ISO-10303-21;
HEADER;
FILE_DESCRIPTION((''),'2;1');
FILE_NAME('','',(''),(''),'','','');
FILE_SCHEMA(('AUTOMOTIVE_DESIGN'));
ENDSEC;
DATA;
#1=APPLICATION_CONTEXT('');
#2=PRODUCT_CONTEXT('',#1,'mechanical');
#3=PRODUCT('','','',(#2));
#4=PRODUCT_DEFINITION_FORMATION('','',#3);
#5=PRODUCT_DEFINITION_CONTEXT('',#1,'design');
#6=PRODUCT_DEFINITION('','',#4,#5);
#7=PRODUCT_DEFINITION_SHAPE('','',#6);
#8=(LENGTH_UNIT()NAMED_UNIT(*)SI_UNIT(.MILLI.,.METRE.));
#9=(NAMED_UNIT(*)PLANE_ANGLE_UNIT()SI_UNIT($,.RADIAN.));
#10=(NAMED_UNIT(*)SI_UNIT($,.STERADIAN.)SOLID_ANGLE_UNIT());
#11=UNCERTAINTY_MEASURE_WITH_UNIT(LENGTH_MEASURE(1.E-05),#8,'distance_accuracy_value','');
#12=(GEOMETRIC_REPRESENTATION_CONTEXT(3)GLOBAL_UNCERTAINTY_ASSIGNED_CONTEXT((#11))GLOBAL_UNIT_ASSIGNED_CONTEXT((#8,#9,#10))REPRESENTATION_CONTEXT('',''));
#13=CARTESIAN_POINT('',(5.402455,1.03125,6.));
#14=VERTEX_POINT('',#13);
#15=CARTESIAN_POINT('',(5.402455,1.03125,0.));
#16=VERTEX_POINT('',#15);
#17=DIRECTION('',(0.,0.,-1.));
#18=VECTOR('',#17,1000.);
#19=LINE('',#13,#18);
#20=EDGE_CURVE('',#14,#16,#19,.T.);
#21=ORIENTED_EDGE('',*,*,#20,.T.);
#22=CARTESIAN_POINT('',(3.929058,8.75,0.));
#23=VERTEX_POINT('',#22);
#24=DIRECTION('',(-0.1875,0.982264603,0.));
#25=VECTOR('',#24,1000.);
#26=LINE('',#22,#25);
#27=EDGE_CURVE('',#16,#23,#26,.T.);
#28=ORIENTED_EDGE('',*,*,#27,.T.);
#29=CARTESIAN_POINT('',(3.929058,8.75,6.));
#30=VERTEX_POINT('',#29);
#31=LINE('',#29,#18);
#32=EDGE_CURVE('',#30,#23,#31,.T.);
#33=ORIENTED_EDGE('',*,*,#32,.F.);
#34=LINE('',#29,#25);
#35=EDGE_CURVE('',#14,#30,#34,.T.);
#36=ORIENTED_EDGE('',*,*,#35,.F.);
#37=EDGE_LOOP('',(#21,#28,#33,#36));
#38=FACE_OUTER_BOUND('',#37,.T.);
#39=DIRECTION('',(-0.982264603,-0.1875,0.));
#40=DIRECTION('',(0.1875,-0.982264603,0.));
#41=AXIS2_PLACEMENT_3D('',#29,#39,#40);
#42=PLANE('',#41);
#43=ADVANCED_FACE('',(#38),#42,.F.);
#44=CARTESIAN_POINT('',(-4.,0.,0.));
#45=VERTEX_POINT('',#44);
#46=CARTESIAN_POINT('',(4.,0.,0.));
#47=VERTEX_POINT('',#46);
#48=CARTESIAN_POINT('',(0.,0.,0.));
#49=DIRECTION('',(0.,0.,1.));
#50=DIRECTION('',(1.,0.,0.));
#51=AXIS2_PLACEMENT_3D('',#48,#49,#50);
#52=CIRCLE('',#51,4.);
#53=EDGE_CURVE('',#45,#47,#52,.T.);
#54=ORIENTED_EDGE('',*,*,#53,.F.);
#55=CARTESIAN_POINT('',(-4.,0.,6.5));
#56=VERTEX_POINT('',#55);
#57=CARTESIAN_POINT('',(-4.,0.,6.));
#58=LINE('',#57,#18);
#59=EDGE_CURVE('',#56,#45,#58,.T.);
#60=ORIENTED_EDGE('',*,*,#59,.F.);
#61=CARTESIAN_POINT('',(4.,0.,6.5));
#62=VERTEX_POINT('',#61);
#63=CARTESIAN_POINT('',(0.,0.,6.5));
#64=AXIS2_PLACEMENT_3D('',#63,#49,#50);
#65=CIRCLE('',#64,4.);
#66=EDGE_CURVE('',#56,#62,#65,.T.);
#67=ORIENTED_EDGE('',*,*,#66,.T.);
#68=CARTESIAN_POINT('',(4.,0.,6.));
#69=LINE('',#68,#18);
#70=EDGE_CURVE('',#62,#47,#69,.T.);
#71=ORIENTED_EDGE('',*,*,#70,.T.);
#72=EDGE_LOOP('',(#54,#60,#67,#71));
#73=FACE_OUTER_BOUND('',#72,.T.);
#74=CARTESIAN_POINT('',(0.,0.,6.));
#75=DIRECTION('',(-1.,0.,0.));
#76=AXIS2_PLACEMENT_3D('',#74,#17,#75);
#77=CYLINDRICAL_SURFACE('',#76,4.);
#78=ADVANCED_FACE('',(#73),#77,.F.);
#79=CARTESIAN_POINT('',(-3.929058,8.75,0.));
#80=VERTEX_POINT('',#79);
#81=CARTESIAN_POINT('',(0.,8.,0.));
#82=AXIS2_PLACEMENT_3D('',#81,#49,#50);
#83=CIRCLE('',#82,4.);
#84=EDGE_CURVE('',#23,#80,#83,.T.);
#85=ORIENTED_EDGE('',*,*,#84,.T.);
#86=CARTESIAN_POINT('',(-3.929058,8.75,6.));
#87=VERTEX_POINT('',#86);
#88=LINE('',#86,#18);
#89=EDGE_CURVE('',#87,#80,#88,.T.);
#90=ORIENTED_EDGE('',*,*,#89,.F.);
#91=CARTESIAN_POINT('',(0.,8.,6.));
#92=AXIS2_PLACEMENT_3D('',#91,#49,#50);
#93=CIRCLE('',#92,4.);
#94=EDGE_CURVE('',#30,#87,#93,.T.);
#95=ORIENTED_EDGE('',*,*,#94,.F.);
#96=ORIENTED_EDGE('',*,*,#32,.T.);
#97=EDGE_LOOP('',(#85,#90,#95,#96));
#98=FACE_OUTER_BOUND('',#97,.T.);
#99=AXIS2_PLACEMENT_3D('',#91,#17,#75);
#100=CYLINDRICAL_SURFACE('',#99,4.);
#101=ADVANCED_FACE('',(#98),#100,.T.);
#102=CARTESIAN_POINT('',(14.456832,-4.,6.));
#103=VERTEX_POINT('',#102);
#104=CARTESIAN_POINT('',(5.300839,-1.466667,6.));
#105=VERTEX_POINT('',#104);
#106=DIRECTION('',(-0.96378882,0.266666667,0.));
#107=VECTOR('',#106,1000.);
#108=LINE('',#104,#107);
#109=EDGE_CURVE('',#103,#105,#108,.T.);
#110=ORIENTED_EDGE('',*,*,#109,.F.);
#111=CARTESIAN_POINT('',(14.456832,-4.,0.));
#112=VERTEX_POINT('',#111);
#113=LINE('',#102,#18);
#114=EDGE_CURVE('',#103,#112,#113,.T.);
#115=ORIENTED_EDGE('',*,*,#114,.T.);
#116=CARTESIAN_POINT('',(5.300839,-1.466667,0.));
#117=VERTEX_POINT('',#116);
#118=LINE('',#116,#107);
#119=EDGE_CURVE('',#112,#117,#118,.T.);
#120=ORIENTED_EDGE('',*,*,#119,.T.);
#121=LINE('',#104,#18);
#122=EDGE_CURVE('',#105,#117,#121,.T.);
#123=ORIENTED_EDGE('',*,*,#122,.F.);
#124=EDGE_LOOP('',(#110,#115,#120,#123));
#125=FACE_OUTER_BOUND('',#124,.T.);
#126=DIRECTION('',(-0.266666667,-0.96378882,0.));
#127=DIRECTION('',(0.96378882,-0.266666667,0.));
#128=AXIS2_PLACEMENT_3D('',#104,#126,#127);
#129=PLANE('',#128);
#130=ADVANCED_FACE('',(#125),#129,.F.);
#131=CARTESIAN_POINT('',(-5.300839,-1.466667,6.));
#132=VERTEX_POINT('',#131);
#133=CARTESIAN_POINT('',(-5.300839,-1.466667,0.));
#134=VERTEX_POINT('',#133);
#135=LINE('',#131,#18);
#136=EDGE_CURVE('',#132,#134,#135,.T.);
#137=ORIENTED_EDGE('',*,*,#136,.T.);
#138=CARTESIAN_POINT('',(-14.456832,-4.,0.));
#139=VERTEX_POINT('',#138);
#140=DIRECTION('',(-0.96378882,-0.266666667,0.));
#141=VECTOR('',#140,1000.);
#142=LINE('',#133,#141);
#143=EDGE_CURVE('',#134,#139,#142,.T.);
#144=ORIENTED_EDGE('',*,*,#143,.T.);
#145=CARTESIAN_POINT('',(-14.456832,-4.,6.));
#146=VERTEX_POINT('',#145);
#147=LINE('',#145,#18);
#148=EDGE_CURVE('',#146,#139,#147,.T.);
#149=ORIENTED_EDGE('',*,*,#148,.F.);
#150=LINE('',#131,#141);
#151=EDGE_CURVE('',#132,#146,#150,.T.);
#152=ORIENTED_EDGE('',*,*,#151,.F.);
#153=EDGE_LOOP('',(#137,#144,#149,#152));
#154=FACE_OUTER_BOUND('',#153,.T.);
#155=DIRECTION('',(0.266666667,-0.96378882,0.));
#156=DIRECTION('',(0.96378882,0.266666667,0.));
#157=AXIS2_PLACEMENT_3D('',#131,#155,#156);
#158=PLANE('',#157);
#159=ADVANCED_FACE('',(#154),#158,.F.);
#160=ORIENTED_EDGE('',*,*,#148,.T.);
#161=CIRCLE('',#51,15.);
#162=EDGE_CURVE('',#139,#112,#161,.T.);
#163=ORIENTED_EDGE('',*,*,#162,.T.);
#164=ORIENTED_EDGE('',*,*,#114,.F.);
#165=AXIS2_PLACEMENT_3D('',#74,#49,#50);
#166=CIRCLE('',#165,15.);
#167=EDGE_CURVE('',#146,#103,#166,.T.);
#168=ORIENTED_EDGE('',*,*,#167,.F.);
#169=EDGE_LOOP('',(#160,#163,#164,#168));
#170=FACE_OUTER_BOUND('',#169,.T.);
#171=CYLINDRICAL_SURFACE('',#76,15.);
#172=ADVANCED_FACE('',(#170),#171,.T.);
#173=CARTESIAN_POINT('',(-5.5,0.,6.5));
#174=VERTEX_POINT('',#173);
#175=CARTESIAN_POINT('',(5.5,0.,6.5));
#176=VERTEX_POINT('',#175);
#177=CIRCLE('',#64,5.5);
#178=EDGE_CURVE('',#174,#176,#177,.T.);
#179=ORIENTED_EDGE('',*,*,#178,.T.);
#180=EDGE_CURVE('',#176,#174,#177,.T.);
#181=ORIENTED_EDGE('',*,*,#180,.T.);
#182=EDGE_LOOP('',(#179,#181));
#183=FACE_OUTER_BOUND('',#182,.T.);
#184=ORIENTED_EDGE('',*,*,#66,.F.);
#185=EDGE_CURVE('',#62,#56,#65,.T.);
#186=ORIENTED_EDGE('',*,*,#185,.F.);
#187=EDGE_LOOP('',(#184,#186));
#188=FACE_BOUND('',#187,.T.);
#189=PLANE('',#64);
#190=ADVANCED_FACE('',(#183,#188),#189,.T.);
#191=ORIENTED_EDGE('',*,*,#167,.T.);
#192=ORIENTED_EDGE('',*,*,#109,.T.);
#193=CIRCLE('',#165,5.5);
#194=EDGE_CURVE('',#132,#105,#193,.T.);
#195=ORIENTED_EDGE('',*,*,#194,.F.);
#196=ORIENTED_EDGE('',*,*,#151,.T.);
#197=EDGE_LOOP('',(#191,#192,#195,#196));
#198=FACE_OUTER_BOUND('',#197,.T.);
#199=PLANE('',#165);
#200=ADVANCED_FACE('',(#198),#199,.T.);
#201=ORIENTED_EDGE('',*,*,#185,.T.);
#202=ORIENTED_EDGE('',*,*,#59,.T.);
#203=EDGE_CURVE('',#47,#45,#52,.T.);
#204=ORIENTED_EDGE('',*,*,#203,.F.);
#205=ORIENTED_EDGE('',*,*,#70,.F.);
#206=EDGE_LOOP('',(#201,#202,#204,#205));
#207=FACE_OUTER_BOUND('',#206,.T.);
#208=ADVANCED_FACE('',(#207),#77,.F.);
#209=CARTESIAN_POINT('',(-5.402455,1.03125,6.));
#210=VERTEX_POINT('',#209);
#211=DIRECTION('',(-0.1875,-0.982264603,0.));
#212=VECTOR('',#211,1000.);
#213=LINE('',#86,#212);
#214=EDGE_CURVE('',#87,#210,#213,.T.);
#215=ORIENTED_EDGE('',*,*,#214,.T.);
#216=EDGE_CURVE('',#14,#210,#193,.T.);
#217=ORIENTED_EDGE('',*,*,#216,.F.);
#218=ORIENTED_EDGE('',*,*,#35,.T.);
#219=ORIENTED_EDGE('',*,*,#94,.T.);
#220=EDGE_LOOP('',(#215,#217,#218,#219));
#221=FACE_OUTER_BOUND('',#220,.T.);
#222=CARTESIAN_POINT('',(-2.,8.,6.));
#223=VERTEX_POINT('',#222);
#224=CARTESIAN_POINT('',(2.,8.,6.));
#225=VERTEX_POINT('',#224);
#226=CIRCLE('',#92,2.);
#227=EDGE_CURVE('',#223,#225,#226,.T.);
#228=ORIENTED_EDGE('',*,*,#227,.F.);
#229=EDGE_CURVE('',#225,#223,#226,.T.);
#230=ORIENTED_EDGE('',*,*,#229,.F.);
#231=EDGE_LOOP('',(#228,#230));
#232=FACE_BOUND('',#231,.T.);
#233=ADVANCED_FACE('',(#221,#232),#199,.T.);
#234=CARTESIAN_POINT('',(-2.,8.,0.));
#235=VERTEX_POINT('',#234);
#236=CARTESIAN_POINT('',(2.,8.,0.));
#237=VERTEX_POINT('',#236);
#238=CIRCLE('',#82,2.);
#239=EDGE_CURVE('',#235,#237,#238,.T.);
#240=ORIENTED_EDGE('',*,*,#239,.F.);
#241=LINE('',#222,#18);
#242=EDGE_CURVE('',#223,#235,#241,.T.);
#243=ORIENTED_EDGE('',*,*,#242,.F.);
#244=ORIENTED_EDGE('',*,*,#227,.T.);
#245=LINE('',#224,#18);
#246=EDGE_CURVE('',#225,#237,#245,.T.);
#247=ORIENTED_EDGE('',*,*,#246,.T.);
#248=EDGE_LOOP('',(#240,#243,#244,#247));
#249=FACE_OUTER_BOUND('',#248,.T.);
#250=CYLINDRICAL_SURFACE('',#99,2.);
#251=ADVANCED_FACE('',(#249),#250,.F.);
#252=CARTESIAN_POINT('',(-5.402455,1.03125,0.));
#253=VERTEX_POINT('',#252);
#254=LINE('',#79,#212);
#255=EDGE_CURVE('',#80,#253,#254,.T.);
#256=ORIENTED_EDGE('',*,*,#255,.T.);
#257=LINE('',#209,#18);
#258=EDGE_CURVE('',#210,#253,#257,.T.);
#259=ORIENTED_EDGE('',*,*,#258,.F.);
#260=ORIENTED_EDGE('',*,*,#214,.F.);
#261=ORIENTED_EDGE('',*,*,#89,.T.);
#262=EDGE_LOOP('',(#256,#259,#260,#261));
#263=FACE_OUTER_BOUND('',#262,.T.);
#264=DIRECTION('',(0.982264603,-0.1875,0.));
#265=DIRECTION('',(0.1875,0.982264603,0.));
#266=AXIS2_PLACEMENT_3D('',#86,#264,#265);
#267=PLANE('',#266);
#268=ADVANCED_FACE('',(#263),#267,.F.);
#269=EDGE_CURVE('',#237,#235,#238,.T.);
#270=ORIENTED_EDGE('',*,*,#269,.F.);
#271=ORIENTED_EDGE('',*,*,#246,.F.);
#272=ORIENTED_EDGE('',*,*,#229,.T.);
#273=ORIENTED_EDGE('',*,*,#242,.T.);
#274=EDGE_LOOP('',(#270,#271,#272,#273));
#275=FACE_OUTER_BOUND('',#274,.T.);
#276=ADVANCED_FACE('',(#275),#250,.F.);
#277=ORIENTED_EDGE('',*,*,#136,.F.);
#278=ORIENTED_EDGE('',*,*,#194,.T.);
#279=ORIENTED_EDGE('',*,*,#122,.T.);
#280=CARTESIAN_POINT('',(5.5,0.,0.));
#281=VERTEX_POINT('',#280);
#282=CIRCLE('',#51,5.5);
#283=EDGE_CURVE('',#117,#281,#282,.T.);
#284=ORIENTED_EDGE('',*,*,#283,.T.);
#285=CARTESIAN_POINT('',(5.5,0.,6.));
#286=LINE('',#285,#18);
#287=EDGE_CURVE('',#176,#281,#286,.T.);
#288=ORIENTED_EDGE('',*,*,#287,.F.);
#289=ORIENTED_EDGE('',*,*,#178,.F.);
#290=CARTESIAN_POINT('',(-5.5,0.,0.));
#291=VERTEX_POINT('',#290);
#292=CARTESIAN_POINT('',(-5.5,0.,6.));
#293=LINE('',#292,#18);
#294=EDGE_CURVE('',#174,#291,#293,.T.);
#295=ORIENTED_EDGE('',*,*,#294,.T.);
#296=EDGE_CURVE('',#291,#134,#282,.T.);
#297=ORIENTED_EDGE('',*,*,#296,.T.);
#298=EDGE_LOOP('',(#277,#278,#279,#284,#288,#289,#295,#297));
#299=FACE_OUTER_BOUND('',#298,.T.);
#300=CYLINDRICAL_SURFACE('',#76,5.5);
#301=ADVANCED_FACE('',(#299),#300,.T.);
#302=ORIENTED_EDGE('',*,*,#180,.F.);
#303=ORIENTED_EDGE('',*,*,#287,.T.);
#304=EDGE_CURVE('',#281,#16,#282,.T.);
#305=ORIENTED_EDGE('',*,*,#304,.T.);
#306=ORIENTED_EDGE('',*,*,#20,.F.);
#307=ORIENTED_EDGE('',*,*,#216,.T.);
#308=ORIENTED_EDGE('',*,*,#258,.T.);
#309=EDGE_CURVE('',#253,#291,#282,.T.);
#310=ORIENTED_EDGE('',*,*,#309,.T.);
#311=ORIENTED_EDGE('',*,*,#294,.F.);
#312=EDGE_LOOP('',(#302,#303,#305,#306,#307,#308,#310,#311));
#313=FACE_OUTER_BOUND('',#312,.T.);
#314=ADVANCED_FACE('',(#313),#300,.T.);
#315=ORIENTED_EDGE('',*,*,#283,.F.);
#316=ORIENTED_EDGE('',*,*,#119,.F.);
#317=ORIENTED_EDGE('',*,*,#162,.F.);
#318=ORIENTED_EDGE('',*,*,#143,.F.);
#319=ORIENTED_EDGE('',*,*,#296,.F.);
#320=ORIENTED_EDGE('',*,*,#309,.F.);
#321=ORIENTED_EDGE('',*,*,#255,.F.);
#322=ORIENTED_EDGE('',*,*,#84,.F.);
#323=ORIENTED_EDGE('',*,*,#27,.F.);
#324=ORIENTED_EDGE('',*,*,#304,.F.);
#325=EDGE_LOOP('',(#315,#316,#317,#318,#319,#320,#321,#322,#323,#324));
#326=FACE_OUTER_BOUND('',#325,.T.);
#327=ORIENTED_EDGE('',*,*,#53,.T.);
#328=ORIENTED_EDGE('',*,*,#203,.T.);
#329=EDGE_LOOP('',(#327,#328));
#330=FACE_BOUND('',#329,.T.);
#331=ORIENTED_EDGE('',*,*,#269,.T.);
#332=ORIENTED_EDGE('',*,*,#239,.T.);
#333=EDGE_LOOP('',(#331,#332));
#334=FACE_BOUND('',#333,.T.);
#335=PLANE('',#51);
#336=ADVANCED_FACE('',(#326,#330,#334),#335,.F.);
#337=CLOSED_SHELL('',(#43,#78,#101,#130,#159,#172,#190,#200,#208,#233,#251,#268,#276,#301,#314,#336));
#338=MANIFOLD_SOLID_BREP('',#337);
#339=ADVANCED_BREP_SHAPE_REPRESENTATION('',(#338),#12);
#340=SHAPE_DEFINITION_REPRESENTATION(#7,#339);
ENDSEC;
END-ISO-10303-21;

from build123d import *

# Parameters (mm, degrees)
SKETCH1_R           = 4
BOSS_EXTRUDE2_DEPTH = 6
SKETCH3_R           = 2
BOSS_EXTRUDE3_DEPTH = 6
SKETCH4_R           = 5.5
SKETCH4_R_2         = 4
BOSS_EXTRUDE4_DEPTH = 0.5


with BuildPart() as part:
    # Sketch1 → Boss-Extrude2 (new body)
    with BuildSketch(Plane.XY):
        with BuildLine():
            Line((-5.300838508, -1.466666667), (-14.456832295, -4))
            ThreePointArc((-14.456832295, -4), (0, -15), (14.456832295, -4))
            Line((14.456832295, -4), (5.300838508, -1.466666667))
            ThreePointArc((5.300838508, -1.466666667), (0, 5.5), (-5.300838508, -1.466666667))
        make_face()
        Circle(SKETCH1_R, mode=Mode.SUBTRACT)
    extrude(amount=BOSS_EXTRUDE2_DEPTH)

    # Sketch3 → Boss-Extrude3 (add)
    with BuildSketch(Plane.XY):
        with BuildLine():
            Line((-3.929058411, 8.75), (-5.402455316, 1.03125))
            ThreePointArc((-5.402455316, 1.03125), (0, 5.5), (5.402455316, 1.03125))
            Line((5.402455316, 1.03125), (3.929058411, 8.75))
            ThreePointArc((3.929058411, 8.75), (0, 12), (-3.929058411, 8.75))
        make_face()
        with Locations((0, 8)):
            Circle(SKETCH3_R, mode=Mode.SUBTRACT)
    extrude(amount=BOSS_EXTRUDE3_DEPTH)

    # Sketch4 → Boss-Extrude4 (add)
    with BuildSketch(Plane.XY.offset(6)):
        with Locations(Location((0, 0, 0), (0, 0, 169.193077125))):
            Circle(SKETCH4_R)
        Circle(SKETCH4_R_2, mode=Mode.SUBTRACT)
    extrude(amount=BOSS_EXTRUDE4_DEPTH)


solid = part.part
